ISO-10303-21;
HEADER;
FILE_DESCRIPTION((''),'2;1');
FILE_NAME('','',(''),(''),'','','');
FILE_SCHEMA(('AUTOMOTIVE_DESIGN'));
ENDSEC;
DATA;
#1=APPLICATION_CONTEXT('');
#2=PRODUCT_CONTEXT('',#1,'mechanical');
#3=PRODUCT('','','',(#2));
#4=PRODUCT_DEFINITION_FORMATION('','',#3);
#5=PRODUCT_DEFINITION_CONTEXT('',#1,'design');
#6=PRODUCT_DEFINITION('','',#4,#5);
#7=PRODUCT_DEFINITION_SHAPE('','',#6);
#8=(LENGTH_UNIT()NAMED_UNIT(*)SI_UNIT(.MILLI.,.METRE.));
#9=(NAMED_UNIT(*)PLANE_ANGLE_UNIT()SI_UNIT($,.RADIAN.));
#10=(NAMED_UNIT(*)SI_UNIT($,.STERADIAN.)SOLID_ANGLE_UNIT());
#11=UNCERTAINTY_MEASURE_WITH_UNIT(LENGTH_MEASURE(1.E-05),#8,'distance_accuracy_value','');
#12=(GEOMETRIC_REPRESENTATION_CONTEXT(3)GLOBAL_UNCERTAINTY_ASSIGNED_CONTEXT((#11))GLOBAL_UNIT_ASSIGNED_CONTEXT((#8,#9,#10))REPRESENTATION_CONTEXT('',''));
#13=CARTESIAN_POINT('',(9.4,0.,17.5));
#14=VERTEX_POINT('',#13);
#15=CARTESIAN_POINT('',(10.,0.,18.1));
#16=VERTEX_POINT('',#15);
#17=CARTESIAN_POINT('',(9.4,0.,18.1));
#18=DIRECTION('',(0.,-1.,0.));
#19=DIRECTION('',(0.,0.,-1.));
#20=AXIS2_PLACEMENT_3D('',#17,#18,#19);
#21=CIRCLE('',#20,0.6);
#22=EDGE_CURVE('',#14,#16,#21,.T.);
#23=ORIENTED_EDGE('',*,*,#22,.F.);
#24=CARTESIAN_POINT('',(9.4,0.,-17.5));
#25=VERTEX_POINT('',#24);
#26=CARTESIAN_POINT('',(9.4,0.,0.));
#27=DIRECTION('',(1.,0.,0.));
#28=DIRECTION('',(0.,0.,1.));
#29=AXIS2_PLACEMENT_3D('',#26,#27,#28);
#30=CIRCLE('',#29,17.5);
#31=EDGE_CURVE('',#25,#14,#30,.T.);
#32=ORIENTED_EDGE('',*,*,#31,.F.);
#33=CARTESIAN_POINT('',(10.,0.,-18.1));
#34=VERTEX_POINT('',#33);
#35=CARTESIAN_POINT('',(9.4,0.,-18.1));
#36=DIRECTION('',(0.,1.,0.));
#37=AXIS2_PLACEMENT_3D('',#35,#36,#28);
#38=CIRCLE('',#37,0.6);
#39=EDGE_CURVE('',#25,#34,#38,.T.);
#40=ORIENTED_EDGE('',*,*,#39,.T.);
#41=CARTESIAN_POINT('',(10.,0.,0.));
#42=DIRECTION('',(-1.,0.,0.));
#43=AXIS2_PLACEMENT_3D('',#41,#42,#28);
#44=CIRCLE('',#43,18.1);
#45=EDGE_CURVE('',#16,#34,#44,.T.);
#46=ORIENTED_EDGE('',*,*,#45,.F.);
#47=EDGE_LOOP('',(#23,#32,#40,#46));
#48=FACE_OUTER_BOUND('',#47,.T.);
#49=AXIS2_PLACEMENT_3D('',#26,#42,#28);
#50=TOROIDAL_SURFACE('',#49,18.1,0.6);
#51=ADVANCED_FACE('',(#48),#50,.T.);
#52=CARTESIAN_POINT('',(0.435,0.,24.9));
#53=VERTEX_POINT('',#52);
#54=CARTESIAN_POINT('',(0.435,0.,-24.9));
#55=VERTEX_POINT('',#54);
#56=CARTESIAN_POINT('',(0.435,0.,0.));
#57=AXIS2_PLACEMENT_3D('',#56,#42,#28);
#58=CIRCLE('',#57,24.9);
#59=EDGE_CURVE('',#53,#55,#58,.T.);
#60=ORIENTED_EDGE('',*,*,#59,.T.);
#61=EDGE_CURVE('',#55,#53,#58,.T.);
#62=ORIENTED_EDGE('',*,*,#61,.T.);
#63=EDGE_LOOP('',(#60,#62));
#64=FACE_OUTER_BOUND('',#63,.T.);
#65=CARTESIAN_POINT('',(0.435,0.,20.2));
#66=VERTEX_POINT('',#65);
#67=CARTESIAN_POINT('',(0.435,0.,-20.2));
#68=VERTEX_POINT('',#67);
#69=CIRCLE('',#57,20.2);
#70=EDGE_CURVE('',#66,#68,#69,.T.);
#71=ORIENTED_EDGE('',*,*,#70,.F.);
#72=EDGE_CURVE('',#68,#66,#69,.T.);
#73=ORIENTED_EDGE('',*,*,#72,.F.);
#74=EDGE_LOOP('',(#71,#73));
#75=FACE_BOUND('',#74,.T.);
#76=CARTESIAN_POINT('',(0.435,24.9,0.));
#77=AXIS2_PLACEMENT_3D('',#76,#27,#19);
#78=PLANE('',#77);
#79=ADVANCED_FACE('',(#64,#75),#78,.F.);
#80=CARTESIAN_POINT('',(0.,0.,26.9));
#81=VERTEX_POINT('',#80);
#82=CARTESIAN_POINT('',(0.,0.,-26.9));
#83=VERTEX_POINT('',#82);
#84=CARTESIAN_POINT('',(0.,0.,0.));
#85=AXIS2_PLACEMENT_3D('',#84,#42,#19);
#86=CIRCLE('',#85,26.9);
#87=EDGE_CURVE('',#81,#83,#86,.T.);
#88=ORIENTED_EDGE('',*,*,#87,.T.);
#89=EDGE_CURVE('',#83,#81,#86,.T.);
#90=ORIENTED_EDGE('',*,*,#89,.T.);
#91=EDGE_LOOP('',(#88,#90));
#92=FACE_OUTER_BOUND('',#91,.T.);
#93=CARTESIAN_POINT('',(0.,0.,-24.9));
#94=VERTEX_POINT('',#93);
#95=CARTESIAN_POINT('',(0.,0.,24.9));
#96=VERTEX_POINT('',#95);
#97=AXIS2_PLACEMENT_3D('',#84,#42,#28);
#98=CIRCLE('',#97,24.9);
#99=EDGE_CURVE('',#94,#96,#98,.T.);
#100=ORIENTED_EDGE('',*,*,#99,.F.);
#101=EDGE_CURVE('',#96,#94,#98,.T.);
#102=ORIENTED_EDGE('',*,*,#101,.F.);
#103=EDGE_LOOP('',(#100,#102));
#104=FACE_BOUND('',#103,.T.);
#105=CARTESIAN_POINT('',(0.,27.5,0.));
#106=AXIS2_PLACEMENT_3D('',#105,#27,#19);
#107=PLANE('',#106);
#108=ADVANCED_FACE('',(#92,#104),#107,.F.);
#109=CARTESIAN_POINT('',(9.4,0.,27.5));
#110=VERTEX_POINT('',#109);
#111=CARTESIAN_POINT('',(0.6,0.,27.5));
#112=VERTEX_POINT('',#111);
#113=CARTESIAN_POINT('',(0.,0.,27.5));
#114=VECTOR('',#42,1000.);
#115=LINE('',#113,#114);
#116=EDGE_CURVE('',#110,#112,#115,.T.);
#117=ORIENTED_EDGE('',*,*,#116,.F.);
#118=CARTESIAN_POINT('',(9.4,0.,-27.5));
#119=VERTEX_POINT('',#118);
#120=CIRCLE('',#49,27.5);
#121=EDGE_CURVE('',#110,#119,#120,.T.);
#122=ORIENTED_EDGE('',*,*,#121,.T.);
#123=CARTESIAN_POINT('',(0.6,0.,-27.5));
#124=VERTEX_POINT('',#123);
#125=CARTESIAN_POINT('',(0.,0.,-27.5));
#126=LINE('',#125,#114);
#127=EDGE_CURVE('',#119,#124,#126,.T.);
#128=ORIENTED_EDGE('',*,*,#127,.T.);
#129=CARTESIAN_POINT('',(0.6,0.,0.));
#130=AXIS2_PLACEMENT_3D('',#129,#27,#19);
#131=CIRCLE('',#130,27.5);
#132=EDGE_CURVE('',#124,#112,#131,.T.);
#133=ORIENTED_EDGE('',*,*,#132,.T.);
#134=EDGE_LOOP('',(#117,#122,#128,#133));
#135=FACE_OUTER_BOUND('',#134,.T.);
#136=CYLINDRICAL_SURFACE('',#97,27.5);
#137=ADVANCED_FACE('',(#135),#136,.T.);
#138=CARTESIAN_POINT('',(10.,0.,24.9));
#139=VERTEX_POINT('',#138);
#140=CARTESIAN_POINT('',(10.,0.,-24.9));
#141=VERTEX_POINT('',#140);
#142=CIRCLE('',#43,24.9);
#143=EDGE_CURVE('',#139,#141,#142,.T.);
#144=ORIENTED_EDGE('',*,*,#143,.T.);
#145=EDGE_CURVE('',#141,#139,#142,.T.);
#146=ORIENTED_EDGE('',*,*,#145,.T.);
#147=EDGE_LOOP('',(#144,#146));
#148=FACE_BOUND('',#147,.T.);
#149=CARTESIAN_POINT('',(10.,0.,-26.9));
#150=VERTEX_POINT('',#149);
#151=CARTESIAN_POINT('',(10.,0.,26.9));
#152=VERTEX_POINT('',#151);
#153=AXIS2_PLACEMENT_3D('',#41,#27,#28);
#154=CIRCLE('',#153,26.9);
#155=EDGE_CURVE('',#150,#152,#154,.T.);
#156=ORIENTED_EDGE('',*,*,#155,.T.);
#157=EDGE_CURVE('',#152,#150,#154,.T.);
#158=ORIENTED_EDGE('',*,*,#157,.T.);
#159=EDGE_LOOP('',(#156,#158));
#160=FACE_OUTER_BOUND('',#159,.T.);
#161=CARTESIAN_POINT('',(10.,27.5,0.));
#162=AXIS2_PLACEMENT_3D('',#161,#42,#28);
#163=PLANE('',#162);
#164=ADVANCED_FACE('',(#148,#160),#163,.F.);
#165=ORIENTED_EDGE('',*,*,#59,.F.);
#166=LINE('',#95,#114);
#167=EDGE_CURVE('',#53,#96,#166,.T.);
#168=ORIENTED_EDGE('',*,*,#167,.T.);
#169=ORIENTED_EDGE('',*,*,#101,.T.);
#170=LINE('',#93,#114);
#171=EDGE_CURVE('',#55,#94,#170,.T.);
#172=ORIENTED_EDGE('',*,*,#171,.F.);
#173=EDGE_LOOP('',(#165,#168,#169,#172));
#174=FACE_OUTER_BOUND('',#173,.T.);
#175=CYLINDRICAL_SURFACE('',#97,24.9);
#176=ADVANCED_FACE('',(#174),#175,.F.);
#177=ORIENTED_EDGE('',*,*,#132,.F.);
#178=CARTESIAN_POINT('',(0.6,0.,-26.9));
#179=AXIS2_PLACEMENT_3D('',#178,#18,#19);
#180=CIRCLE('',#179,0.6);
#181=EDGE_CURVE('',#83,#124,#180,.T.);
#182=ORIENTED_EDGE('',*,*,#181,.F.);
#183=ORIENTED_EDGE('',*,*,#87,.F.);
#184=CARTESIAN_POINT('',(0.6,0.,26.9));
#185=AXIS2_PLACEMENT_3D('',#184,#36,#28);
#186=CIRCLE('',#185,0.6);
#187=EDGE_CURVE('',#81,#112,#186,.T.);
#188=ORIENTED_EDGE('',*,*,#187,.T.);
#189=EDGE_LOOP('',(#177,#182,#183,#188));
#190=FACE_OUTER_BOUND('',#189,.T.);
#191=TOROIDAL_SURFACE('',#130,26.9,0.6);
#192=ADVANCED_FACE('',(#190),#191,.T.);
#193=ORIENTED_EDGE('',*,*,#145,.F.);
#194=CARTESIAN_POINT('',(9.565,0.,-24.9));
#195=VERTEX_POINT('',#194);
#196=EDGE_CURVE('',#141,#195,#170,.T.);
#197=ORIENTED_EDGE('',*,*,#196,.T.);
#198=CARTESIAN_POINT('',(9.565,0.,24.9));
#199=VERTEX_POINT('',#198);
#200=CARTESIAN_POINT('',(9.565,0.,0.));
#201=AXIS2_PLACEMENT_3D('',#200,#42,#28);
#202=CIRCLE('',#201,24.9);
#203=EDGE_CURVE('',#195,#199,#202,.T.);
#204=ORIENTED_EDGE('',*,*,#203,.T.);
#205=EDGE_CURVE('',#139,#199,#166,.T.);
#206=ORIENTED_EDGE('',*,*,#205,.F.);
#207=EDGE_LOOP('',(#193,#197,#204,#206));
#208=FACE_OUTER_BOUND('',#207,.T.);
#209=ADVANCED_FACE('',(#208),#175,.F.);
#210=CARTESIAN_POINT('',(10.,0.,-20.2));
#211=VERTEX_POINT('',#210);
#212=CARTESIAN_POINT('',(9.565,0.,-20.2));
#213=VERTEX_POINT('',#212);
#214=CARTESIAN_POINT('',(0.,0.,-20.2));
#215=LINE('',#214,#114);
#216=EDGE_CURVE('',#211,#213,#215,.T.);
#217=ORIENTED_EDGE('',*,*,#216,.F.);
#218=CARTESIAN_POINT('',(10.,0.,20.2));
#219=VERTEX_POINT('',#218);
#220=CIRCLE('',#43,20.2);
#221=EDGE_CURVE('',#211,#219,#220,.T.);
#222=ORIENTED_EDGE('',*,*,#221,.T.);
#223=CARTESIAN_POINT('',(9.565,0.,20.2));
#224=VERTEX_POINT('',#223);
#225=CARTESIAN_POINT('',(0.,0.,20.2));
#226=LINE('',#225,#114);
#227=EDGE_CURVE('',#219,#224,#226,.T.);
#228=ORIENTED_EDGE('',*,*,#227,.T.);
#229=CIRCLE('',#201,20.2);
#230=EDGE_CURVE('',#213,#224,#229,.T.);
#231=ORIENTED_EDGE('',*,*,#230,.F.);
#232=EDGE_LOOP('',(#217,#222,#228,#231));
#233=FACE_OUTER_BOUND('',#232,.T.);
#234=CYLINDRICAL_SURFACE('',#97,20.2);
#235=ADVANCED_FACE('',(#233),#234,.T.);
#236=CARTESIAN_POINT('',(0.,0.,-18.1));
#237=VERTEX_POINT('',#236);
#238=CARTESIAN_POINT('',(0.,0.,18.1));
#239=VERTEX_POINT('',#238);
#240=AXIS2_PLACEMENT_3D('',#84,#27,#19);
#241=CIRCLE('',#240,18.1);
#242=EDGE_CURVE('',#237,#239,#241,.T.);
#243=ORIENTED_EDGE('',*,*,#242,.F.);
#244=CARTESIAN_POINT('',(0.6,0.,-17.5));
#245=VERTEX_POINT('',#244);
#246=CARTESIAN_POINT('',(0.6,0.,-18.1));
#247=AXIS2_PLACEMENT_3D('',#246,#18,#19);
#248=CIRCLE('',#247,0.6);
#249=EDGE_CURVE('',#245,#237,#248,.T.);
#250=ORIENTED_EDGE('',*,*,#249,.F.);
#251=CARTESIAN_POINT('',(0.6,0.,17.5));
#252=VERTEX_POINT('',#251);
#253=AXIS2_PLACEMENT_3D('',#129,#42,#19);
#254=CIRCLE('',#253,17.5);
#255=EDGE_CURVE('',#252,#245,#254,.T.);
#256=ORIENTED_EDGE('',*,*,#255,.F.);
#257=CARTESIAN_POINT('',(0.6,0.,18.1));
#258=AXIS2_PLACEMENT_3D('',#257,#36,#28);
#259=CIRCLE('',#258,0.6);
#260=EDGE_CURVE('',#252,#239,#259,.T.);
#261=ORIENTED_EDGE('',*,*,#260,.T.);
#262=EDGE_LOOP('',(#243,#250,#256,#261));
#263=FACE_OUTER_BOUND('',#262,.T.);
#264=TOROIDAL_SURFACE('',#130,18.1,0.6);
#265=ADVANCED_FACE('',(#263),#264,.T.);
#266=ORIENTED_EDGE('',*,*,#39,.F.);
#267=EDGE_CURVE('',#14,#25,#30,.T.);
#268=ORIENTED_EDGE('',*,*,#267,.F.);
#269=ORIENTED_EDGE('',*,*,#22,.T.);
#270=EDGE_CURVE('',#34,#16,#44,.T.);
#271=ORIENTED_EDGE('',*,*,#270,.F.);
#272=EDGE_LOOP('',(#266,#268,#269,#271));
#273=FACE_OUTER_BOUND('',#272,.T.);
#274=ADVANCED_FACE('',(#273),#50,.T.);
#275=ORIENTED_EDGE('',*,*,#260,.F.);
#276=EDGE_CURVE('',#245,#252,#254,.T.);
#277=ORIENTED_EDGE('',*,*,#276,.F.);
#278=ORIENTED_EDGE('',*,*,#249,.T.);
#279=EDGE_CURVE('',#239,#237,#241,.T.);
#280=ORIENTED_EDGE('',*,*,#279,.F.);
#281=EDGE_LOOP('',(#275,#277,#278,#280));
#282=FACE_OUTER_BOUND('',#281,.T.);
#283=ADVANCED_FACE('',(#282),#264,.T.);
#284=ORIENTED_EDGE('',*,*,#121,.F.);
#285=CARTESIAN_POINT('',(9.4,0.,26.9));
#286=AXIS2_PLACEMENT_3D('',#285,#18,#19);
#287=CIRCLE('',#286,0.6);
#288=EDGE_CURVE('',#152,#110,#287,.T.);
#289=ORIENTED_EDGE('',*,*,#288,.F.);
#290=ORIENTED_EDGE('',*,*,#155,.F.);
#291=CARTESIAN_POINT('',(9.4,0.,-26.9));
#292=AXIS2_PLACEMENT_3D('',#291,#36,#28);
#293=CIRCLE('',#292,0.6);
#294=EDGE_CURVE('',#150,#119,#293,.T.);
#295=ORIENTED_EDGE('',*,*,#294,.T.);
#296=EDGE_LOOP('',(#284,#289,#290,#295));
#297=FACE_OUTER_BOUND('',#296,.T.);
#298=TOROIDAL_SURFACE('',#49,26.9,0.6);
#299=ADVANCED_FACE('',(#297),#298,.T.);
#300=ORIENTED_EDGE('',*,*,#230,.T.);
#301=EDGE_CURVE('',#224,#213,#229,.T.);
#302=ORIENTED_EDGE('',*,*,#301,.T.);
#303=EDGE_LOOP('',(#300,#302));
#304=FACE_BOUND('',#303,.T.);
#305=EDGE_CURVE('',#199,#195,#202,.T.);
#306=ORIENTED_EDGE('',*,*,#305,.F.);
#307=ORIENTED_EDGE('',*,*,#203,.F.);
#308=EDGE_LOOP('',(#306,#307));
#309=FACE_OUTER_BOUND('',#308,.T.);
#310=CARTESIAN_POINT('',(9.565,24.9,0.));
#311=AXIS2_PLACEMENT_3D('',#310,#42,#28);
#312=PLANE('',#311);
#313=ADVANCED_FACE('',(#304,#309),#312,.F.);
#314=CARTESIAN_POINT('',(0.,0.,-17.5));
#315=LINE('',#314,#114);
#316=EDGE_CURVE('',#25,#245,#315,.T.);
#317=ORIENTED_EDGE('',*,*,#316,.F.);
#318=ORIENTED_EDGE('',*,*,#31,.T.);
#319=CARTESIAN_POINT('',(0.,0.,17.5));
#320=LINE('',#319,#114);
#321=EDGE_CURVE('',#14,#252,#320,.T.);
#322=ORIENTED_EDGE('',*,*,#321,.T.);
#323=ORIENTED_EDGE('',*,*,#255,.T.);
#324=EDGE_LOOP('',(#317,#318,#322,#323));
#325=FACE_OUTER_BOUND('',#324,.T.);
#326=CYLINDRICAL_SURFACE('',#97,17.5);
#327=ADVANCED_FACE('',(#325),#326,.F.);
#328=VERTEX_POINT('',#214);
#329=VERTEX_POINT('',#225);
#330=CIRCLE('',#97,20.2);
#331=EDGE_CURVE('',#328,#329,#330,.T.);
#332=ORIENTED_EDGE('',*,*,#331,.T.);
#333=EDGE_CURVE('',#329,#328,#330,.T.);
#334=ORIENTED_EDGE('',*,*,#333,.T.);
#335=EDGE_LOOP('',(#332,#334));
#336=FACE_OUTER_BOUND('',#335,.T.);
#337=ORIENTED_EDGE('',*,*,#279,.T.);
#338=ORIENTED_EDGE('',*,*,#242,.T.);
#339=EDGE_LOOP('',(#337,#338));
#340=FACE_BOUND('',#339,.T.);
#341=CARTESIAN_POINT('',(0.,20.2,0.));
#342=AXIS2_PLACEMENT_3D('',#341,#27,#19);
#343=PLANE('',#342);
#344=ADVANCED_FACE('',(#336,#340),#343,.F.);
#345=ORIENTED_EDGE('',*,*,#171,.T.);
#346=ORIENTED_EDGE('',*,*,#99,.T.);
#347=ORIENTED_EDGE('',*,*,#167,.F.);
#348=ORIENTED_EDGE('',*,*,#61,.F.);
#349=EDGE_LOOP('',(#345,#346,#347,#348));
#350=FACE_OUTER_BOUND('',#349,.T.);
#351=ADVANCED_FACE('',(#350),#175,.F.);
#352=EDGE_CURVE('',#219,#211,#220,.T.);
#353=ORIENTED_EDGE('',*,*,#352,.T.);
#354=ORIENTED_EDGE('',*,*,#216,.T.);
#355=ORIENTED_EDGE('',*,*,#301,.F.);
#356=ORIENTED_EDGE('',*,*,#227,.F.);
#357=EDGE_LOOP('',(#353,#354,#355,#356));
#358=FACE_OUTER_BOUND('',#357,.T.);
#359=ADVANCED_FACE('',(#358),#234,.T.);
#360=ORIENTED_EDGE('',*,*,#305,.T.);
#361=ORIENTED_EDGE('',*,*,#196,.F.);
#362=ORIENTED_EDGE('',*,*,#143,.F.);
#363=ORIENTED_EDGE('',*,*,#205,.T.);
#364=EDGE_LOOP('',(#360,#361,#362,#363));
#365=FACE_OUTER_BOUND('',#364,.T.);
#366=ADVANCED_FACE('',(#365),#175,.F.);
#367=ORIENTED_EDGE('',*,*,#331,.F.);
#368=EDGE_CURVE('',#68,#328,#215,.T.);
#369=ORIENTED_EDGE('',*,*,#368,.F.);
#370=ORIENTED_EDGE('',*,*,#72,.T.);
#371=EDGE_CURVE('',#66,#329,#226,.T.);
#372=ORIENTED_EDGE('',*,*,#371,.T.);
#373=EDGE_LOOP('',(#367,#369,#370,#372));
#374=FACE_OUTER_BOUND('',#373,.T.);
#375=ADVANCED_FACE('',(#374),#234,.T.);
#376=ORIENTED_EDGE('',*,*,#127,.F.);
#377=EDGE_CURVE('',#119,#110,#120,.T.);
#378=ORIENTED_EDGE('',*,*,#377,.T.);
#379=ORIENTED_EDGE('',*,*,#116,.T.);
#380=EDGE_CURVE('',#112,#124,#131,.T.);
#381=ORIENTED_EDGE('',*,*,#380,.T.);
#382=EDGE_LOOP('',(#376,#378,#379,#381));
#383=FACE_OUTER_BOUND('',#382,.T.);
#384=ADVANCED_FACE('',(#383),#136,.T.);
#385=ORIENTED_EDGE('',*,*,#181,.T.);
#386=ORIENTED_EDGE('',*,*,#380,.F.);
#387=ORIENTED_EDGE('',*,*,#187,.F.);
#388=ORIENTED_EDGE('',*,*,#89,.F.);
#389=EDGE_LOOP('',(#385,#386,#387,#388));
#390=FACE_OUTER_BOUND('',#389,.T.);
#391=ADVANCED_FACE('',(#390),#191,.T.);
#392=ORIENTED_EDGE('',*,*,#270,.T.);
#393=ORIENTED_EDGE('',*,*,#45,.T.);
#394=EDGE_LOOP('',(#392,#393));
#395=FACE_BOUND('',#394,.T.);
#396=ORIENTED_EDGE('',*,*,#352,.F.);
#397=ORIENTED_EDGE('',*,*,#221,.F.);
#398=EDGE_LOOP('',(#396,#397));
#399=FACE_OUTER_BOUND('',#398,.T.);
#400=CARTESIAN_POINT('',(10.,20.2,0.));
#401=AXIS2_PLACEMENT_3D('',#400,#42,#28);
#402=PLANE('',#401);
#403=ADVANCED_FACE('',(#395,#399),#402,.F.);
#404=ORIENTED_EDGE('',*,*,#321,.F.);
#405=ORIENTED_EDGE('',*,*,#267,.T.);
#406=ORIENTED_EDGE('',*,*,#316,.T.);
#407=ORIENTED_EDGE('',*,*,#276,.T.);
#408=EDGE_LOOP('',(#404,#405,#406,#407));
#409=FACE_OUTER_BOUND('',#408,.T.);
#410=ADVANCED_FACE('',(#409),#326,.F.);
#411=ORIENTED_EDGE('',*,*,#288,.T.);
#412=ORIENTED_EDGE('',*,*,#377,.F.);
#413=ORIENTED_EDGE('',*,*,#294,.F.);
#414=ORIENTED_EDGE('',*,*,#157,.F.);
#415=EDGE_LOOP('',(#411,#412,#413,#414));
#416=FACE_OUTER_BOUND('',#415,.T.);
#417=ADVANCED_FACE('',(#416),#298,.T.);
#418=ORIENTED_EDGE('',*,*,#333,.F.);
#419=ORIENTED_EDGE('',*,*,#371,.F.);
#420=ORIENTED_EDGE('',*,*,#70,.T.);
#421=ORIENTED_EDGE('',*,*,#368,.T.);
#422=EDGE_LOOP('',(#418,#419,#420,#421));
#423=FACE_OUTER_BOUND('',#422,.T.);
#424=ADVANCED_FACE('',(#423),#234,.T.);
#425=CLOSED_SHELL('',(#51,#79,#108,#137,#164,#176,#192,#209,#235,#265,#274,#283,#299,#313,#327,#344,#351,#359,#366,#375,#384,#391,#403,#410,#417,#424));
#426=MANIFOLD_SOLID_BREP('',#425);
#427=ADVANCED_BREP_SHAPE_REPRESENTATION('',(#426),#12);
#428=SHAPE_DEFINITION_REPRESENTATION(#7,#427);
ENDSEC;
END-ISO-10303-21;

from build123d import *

# Parameters (mm, degrees)
FILLET1_R = 0.6
FILLET2_R = 0.6


with BuildPart() as part:
    # Sketch1 → Revolve1 (revolve)
    with BuildSketch(Plane.XY, mode=Mode.PRIVATE) as revolve1_sk:
        Polygon((0, 17.5), (10, 17.5), (10, 20.2), (9.565, 20.2), (9.565, 24.9), (10, 24.9), (10, 27.5), (0, 27.5), (0, 24.9), (0.435, 24.9), (0.435, 20.2), (0, 20.2), align=None)
    revolve(revolve1_sk.sketch.rotate(Axis((0, 0, 0), (1, 0, 0)), 90), axis=Axis((0, 0, 0), (1, 0, 0)))

    # Fillet1
    fillet1_edges = [part.edges().sort_by_distance(p)[0] for p in [
        (0, 0, -27.5),
        (10, 0, -27.5),
    ]]
    fillet(fillet1_edges, radius=FILLET1_R)

    # Fillet2
    fillet2_edges = [part.edges().sort_by_distance(p)[0] for p in [
        (10, 0, -17.5),
        (0, 0, -17.5),
    ]]
    fillet(fillet2_edges, radius=FILLET2_R)


solid = part.part
